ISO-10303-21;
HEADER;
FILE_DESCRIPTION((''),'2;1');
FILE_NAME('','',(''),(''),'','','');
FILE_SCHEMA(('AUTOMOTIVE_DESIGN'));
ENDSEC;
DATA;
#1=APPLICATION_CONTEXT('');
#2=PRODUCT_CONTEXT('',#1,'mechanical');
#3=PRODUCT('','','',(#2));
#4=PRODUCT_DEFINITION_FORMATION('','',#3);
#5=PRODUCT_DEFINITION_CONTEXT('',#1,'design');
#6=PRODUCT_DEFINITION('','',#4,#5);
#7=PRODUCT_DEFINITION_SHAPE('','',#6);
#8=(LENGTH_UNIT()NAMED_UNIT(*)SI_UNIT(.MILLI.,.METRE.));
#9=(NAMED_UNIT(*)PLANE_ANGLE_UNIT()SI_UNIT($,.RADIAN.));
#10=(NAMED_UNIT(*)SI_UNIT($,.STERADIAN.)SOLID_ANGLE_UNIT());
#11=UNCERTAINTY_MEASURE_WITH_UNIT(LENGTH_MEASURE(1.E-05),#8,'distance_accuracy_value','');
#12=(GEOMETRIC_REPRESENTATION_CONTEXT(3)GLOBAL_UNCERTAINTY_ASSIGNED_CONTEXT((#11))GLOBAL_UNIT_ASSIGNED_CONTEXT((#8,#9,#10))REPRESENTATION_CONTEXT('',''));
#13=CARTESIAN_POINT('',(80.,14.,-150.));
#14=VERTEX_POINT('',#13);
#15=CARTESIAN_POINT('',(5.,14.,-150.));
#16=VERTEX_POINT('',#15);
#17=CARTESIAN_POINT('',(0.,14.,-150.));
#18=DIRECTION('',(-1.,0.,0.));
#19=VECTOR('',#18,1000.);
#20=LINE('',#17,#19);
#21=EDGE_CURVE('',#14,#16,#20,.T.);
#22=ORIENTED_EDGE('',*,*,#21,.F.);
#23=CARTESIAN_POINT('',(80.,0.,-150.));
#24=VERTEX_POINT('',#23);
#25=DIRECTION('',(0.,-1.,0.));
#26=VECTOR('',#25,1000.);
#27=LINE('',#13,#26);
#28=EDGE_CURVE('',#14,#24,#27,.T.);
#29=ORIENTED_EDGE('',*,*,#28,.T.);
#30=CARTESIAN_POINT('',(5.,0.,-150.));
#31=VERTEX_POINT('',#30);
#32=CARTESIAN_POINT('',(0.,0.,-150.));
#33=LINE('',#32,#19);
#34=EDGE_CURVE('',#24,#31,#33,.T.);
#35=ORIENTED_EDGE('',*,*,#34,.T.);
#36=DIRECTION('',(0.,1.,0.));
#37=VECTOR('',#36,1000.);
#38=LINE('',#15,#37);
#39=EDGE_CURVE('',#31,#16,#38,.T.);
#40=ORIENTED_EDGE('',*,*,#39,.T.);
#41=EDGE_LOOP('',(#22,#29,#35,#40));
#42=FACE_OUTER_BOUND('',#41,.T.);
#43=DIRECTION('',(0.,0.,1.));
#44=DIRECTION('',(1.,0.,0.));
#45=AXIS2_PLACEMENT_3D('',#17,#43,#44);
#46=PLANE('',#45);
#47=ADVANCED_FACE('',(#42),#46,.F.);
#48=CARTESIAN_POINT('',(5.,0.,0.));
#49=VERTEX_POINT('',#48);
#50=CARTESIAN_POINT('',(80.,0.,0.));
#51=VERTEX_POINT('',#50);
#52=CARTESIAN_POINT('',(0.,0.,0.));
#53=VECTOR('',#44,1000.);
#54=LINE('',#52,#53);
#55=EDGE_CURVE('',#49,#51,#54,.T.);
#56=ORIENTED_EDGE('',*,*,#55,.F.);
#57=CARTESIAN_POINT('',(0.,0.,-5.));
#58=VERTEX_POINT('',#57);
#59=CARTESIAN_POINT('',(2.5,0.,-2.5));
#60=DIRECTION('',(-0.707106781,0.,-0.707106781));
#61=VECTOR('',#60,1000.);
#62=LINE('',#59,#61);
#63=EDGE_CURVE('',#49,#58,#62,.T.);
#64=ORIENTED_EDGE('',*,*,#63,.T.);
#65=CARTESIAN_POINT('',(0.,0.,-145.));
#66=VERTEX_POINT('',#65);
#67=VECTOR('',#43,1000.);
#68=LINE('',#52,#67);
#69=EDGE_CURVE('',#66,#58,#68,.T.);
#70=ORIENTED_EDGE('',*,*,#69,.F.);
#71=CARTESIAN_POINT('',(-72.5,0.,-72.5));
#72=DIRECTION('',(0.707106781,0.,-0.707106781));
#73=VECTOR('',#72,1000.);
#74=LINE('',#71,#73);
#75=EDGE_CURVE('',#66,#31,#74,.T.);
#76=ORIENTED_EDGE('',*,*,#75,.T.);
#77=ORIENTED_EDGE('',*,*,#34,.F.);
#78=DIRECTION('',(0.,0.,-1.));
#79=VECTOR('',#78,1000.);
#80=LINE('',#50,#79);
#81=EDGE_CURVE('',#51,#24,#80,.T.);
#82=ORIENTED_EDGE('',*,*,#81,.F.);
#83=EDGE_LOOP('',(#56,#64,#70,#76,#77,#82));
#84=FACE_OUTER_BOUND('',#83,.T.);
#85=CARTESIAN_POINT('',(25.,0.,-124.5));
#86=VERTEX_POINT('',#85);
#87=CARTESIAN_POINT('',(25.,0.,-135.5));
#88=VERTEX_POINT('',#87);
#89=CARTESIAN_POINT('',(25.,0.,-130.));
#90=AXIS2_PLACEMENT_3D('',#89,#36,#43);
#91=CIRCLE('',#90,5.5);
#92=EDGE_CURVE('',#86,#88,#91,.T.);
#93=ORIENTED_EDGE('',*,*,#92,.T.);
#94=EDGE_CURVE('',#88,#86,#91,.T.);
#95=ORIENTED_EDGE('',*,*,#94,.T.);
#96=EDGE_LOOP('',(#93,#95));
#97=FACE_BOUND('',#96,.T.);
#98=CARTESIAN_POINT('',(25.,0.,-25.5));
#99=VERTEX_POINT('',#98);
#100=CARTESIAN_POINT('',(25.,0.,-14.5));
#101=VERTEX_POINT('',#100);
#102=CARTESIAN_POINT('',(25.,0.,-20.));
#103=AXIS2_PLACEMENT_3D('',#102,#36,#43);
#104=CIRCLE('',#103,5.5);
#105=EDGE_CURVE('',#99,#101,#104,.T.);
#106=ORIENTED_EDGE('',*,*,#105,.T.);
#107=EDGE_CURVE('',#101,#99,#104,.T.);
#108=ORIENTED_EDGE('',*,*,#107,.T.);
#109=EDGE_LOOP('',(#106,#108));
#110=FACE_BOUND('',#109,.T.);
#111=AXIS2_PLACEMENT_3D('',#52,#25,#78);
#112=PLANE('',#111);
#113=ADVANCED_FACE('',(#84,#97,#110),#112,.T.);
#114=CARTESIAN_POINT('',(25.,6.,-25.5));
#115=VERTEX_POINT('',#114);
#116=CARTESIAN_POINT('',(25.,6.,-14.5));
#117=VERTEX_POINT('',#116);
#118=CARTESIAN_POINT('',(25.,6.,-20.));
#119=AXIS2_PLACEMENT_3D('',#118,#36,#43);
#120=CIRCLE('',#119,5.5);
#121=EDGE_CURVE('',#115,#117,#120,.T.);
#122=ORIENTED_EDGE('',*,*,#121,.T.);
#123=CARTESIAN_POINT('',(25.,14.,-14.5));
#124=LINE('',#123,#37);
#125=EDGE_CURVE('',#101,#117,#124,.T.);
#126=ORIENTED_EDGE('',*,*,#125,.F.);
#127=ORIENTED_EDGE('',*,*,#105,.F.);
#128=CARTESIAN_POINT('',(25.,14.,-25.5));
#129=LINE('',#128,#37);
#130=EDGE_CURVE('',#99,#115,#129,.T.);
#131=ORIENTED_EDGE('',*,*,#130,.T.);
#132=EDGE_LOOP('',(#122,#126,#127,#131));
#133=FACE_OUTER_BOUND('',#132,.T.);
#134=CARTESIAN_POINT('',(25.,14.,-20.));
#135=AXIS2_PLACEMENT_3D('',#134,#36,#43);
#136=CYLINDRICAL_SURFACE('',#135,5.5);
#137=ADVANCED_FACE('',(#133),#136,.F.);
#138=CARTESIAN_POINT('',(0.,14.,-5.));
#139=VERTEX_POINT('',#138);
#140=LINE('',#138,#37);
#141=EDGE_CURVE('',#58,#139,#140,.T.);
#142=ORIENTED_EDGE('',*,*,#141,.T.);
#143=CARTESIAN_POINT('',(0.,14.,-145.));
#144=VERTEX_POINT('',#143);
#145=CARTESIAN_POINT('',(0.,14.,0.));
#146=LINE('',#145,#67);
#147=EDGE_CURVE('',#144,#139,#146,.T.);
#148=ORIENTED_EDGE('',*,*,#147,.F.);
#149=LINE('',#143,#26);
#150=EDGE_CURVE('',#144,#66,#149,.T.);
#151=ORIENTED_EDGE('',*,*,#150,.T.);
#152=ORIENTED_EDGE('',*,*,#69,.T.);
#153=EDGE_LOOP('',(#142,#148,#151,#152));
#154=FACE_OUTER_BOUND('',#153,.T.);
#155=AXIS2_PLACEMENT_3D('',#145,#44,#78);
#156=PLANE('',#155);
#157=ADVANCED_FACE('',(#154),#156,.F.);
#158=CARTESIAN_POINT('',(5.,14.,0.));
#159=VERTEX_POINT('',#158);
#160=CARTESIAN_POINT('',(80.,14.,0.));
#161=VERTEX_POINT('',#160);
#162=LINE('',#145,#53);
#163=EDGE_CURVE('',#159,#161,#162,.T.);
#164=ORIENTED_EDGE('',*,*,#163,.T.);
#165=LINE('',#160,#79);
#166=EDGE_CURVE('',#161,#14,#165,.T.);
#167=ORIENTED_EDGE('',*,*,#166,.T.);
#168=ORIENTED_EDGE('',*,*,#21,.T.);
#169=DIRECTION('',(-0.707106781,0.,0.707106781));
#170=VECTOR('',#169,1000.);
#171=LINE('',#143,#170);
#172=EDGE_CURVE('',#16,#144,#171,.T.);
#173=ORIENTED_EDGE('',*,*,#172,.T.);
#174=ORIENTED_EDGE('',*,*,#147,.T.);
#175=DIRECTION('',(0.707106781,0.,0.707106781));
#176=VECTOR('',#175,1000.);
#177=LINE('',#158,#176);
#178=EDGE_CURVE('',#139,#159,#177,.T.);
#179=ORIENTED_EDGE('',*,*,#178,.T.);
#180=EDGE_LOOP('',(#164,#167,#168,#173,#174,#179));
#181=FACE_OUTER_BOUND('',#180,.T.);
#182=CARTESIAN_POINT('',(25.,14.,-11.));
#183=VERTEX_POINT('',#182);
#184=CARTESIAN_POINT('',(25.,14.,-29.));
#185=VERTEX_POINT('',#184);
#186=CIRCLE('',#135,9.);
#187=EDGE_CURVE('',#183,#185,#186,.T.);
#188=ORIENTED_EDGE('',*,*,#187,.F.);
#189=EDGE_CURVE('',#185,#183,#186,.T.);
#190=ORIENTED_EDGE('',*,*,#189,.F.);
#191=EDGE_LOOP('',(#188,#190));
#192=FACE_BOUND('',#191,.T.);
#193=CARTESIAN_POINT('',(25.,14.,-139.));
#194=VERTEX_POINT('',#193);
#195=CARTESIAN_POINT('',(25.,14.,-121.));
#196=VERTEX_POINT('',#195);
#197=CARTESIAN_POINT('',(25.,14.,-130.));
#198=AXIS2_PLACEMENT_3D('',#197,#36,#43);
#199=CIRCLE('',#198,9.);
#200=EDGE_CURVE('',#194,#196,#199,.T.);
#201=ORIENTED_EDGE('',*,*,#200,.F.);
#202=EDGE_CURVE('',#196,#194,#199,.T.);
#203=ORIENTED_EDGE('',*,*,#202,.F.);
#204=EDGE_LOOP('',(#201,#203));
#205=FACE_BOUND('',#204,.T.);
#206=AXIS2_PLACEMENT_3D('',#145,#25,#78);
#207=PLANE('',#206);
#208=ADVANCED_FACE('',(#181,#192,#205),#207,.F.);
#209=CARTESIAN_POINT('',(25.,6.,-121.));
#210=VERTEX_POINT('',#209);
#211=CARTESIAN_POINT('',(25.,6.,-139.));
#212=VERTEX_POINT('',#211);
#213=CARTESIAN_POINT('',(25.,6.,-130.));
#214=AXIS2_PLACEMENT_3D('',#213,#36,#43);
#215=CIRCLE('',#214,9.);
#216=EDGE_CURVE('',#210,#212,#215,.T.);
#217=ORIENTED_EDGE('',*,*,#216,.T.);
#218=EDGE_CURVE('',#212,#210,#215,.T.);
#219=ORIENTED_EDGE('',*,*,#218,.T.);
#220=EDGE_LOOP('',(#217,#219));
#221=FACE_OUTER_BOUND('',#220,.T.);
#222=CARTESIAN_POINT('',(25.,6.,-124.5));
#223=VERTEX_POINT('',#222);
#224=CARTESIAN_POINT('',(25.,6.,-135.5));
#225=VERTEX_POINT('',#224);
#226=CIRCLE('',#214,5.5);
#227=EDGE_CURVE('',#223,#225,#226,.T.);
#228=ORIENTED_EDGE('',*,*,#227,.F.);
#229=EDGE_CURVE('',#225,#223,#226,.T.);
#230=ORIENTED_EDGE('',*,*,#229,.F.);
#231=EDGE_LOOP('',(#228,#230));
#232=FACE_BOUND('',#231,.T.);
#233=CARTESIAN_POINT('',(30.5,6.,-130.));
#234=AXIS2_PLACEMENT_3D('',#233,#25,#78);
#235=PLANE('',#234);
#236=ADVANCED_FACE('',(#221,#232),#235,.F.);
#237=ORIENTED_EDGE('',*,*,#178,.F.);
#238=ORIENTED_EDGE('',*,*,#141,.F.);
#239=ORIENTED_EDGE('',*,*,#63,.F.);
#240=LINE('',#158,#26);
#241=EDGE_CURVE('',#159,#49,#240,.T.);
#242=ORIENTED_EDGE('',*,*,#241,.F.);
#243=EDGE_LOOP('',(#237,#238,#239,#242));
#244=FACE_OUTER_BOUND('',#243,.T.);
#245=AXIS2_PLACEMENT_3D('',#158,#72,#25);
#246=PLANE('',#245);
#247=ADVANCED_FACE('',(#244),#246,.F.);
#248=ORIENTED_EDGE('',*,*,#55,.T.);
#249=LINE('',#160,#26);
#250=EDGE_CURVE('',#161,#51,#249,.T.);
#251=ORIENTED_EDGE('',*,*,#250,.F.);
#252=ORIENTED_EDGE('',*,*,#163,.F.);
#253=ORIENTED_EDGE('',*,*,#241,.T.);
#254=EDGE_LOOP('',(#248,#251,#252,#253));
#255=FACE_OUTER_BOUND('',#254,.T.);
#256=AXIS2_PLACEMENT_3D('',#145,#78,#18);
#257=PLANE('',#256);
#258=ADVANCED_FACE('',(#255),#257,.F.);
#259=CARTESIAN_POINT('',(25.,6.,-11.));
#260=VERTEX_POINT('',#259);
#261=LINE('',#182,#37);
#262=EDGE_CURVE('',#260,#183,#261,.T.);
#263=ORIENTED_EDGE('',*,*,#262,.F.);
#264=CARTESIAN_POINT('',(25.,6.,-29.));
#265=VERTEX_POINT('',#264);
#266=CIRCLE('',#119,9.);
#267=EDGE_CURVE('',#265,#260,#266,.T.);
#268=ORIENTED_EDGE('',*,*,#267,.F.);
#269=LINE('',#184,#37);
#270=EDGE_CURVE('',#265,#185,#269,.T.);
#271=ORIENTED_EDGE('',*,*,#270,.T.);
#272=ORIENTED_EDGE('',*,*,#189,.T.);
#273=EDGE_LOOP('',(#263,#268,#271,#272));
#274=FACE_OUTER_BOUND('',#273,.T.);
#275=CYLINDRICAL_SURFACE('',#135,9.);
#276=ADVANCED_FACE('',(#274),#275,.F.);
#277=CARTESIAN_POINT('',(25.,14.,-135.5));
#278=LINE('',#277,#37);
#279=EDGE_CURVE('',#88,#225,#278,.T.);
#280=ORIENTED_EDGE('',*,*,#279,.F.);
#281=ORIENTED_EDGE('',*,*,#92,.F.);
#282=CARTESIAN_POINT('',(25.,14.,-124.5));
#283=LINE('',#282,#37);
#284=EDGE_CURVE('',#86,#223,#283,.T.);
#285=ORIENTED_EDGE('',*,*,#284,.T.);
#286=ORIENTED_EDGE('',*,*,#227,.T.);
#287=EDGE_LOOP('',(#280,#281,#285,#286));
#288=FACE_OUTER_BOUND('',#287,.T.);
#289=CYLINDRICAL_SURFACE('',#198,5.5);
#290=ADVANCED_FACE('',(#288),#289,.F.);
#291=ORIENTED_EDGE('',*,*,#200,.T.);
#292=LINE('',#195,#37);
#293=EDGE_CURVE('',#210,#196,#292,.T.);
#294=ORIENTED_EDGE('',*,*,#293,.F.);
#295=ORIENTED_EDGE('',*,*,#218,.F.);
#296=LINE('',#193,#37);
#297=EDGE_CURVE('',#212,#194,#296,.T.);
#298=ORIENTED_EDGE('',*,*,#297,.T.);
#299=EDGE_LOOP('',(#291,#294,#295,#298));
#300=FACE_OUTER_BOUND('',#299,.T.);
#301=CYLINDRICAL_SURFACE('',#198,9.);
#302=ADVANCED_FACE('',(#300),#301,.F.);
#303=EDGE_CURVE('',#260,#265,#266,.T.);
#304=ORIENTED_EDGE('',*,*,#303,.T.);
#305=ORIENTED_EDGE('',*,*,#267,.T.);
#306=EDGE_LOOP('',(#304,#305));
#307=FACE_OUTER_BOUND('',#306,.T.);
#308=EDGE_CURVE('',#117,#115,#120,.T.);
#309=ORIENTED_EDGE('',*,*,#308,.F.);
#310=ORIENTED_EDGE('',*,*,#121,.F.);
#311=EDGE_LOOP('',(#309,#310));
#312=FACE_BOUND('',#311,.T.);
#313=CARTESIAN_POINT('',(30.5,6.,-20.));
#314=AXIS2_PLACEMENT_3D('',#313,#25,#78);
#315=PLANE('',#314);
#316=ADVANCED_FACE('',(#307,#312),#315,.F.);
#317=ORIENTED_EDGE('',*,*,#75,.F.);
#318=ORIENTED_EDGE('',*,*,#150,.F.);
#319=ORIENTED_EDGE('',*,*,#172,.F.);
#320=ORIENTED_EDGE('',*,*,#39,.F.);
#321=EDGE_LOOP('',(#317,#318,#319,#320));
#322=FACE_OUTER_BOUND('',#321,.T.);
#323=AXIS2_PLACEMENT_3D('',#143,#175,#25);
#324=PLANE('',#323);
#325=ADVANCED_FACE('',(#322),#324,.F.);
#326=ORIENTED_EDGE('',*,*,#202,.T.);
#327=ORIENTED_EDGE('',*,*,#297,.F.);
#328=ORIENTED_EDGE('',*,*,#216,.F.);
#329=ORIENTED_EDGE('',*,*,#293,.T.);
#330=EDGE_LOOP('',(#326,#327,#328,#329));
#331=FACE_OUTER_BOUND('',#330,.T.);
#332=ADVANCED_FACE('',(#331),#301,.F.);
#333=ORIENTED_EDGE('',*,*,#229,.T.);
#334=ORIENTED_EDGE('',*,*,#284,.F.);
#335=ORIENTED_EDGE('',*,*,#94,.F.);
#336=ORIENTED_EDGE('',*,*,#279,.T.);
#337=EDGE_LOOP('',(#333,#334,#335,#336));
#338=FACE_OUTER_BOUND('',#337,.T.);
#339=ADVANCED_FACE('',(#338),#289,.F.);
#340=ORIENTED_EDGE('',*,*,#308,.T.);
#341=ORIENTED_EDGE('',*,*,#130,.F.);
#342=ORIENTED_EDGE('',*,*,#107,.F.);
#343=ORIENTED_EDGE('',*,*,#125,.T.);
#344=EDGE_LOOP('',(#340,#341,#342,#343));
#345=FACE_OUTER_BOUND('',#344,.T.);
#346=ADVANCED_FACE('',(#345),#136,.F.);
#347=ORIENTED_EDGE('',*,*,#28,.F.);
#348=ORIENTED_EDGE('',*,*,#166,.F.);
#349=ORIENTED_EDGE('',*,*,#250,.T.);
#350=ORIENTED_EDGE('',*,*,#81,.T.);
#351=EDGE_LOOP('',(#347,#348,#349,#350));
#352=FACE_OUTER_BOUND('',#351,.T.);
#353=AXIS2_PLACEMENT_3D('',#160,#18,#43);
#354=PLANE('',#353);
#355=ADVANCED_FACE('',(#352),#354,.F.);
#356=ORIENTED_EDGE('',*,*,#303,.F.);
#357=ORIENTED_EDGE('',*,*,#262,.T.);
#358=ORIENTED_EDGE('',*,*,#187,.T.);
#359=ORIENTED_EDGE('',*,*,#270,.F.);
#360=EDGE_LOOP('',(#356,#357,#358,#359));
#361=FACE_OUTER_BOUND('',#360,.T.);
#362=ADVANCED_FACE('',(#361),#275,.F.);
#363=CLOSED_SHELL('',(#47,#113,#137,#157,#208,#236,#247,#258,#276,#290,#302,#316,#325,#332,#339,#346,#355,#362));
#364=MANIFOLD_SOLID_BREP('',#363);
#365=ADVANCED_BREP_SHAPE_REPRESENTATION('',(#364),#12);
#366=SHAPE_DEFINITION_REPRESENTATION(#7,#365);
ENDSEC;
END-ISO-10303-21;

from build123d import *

# Parameters (mm, degrees)
SKETCH1_W                                           = 80
SKETCH1_H                                           = 150
BOSS_EXTRUDE1_DEPTH                                 = 14
HOLE_SIZE_BY_SOCKET_HEAD_CAP_SCREW_TYPE_D           = 11
HOLE_SIZE_BY_SOCKET_HEAD_CAP_SCREW_TYPE_CBORE_D     = 18
HOLE_SIZE_BY_SOCKET_HEAD_CAP_SCREW_TYPE_CBORE_DEPTH = 8
CHAMFER1_SIZE                                       = 5


with BuildPart() as part:
    # Sketch1 → Boss-Extrude1 (new body)
    with BuildSketch(Plane(origin=(0, 0, 0), x_dir=(1, 0, 0), z_dir=(0, 1, 0))):
        with Locations((40, 75)):
            Rectangle(SKETCH1_W, SKETCH1_H)
    extrude(amount=BOSS_EXTRUDE1_DEPTH)

    # Hole size (by socket head cap screw type)1 (through all)
    with Locations(Plane(origin=(0, 14, 0), x_dir=(1, 0, 0), z_dir=(0, 1, 0))):
        with Locations((25, 130), (25, 20)):
            CounterBoreHole(HOLE_SIZE_BY_SOCKET_HEAD_CAP_SCREW_TYPE_D / 2, HOLE_SIZE_BY_SOCKET_HEAD_CAP_SCREW_TYPE_CBORE_D / 2, HOLE_SIZE_BY_SOCKET_HEAD_CAP_SCREW_TYPE_CBORE_DEPTH)

    # Chamfer1
    chamfer1_edges = [part.edges().sort_by_distance(p)[0] for p in [
        (0, 7, -150),
        (0, 7, 0),
    ]]
    chamfer(chamfer1_edges, length=CHAMFER1_SIZE)


solid = part.part
